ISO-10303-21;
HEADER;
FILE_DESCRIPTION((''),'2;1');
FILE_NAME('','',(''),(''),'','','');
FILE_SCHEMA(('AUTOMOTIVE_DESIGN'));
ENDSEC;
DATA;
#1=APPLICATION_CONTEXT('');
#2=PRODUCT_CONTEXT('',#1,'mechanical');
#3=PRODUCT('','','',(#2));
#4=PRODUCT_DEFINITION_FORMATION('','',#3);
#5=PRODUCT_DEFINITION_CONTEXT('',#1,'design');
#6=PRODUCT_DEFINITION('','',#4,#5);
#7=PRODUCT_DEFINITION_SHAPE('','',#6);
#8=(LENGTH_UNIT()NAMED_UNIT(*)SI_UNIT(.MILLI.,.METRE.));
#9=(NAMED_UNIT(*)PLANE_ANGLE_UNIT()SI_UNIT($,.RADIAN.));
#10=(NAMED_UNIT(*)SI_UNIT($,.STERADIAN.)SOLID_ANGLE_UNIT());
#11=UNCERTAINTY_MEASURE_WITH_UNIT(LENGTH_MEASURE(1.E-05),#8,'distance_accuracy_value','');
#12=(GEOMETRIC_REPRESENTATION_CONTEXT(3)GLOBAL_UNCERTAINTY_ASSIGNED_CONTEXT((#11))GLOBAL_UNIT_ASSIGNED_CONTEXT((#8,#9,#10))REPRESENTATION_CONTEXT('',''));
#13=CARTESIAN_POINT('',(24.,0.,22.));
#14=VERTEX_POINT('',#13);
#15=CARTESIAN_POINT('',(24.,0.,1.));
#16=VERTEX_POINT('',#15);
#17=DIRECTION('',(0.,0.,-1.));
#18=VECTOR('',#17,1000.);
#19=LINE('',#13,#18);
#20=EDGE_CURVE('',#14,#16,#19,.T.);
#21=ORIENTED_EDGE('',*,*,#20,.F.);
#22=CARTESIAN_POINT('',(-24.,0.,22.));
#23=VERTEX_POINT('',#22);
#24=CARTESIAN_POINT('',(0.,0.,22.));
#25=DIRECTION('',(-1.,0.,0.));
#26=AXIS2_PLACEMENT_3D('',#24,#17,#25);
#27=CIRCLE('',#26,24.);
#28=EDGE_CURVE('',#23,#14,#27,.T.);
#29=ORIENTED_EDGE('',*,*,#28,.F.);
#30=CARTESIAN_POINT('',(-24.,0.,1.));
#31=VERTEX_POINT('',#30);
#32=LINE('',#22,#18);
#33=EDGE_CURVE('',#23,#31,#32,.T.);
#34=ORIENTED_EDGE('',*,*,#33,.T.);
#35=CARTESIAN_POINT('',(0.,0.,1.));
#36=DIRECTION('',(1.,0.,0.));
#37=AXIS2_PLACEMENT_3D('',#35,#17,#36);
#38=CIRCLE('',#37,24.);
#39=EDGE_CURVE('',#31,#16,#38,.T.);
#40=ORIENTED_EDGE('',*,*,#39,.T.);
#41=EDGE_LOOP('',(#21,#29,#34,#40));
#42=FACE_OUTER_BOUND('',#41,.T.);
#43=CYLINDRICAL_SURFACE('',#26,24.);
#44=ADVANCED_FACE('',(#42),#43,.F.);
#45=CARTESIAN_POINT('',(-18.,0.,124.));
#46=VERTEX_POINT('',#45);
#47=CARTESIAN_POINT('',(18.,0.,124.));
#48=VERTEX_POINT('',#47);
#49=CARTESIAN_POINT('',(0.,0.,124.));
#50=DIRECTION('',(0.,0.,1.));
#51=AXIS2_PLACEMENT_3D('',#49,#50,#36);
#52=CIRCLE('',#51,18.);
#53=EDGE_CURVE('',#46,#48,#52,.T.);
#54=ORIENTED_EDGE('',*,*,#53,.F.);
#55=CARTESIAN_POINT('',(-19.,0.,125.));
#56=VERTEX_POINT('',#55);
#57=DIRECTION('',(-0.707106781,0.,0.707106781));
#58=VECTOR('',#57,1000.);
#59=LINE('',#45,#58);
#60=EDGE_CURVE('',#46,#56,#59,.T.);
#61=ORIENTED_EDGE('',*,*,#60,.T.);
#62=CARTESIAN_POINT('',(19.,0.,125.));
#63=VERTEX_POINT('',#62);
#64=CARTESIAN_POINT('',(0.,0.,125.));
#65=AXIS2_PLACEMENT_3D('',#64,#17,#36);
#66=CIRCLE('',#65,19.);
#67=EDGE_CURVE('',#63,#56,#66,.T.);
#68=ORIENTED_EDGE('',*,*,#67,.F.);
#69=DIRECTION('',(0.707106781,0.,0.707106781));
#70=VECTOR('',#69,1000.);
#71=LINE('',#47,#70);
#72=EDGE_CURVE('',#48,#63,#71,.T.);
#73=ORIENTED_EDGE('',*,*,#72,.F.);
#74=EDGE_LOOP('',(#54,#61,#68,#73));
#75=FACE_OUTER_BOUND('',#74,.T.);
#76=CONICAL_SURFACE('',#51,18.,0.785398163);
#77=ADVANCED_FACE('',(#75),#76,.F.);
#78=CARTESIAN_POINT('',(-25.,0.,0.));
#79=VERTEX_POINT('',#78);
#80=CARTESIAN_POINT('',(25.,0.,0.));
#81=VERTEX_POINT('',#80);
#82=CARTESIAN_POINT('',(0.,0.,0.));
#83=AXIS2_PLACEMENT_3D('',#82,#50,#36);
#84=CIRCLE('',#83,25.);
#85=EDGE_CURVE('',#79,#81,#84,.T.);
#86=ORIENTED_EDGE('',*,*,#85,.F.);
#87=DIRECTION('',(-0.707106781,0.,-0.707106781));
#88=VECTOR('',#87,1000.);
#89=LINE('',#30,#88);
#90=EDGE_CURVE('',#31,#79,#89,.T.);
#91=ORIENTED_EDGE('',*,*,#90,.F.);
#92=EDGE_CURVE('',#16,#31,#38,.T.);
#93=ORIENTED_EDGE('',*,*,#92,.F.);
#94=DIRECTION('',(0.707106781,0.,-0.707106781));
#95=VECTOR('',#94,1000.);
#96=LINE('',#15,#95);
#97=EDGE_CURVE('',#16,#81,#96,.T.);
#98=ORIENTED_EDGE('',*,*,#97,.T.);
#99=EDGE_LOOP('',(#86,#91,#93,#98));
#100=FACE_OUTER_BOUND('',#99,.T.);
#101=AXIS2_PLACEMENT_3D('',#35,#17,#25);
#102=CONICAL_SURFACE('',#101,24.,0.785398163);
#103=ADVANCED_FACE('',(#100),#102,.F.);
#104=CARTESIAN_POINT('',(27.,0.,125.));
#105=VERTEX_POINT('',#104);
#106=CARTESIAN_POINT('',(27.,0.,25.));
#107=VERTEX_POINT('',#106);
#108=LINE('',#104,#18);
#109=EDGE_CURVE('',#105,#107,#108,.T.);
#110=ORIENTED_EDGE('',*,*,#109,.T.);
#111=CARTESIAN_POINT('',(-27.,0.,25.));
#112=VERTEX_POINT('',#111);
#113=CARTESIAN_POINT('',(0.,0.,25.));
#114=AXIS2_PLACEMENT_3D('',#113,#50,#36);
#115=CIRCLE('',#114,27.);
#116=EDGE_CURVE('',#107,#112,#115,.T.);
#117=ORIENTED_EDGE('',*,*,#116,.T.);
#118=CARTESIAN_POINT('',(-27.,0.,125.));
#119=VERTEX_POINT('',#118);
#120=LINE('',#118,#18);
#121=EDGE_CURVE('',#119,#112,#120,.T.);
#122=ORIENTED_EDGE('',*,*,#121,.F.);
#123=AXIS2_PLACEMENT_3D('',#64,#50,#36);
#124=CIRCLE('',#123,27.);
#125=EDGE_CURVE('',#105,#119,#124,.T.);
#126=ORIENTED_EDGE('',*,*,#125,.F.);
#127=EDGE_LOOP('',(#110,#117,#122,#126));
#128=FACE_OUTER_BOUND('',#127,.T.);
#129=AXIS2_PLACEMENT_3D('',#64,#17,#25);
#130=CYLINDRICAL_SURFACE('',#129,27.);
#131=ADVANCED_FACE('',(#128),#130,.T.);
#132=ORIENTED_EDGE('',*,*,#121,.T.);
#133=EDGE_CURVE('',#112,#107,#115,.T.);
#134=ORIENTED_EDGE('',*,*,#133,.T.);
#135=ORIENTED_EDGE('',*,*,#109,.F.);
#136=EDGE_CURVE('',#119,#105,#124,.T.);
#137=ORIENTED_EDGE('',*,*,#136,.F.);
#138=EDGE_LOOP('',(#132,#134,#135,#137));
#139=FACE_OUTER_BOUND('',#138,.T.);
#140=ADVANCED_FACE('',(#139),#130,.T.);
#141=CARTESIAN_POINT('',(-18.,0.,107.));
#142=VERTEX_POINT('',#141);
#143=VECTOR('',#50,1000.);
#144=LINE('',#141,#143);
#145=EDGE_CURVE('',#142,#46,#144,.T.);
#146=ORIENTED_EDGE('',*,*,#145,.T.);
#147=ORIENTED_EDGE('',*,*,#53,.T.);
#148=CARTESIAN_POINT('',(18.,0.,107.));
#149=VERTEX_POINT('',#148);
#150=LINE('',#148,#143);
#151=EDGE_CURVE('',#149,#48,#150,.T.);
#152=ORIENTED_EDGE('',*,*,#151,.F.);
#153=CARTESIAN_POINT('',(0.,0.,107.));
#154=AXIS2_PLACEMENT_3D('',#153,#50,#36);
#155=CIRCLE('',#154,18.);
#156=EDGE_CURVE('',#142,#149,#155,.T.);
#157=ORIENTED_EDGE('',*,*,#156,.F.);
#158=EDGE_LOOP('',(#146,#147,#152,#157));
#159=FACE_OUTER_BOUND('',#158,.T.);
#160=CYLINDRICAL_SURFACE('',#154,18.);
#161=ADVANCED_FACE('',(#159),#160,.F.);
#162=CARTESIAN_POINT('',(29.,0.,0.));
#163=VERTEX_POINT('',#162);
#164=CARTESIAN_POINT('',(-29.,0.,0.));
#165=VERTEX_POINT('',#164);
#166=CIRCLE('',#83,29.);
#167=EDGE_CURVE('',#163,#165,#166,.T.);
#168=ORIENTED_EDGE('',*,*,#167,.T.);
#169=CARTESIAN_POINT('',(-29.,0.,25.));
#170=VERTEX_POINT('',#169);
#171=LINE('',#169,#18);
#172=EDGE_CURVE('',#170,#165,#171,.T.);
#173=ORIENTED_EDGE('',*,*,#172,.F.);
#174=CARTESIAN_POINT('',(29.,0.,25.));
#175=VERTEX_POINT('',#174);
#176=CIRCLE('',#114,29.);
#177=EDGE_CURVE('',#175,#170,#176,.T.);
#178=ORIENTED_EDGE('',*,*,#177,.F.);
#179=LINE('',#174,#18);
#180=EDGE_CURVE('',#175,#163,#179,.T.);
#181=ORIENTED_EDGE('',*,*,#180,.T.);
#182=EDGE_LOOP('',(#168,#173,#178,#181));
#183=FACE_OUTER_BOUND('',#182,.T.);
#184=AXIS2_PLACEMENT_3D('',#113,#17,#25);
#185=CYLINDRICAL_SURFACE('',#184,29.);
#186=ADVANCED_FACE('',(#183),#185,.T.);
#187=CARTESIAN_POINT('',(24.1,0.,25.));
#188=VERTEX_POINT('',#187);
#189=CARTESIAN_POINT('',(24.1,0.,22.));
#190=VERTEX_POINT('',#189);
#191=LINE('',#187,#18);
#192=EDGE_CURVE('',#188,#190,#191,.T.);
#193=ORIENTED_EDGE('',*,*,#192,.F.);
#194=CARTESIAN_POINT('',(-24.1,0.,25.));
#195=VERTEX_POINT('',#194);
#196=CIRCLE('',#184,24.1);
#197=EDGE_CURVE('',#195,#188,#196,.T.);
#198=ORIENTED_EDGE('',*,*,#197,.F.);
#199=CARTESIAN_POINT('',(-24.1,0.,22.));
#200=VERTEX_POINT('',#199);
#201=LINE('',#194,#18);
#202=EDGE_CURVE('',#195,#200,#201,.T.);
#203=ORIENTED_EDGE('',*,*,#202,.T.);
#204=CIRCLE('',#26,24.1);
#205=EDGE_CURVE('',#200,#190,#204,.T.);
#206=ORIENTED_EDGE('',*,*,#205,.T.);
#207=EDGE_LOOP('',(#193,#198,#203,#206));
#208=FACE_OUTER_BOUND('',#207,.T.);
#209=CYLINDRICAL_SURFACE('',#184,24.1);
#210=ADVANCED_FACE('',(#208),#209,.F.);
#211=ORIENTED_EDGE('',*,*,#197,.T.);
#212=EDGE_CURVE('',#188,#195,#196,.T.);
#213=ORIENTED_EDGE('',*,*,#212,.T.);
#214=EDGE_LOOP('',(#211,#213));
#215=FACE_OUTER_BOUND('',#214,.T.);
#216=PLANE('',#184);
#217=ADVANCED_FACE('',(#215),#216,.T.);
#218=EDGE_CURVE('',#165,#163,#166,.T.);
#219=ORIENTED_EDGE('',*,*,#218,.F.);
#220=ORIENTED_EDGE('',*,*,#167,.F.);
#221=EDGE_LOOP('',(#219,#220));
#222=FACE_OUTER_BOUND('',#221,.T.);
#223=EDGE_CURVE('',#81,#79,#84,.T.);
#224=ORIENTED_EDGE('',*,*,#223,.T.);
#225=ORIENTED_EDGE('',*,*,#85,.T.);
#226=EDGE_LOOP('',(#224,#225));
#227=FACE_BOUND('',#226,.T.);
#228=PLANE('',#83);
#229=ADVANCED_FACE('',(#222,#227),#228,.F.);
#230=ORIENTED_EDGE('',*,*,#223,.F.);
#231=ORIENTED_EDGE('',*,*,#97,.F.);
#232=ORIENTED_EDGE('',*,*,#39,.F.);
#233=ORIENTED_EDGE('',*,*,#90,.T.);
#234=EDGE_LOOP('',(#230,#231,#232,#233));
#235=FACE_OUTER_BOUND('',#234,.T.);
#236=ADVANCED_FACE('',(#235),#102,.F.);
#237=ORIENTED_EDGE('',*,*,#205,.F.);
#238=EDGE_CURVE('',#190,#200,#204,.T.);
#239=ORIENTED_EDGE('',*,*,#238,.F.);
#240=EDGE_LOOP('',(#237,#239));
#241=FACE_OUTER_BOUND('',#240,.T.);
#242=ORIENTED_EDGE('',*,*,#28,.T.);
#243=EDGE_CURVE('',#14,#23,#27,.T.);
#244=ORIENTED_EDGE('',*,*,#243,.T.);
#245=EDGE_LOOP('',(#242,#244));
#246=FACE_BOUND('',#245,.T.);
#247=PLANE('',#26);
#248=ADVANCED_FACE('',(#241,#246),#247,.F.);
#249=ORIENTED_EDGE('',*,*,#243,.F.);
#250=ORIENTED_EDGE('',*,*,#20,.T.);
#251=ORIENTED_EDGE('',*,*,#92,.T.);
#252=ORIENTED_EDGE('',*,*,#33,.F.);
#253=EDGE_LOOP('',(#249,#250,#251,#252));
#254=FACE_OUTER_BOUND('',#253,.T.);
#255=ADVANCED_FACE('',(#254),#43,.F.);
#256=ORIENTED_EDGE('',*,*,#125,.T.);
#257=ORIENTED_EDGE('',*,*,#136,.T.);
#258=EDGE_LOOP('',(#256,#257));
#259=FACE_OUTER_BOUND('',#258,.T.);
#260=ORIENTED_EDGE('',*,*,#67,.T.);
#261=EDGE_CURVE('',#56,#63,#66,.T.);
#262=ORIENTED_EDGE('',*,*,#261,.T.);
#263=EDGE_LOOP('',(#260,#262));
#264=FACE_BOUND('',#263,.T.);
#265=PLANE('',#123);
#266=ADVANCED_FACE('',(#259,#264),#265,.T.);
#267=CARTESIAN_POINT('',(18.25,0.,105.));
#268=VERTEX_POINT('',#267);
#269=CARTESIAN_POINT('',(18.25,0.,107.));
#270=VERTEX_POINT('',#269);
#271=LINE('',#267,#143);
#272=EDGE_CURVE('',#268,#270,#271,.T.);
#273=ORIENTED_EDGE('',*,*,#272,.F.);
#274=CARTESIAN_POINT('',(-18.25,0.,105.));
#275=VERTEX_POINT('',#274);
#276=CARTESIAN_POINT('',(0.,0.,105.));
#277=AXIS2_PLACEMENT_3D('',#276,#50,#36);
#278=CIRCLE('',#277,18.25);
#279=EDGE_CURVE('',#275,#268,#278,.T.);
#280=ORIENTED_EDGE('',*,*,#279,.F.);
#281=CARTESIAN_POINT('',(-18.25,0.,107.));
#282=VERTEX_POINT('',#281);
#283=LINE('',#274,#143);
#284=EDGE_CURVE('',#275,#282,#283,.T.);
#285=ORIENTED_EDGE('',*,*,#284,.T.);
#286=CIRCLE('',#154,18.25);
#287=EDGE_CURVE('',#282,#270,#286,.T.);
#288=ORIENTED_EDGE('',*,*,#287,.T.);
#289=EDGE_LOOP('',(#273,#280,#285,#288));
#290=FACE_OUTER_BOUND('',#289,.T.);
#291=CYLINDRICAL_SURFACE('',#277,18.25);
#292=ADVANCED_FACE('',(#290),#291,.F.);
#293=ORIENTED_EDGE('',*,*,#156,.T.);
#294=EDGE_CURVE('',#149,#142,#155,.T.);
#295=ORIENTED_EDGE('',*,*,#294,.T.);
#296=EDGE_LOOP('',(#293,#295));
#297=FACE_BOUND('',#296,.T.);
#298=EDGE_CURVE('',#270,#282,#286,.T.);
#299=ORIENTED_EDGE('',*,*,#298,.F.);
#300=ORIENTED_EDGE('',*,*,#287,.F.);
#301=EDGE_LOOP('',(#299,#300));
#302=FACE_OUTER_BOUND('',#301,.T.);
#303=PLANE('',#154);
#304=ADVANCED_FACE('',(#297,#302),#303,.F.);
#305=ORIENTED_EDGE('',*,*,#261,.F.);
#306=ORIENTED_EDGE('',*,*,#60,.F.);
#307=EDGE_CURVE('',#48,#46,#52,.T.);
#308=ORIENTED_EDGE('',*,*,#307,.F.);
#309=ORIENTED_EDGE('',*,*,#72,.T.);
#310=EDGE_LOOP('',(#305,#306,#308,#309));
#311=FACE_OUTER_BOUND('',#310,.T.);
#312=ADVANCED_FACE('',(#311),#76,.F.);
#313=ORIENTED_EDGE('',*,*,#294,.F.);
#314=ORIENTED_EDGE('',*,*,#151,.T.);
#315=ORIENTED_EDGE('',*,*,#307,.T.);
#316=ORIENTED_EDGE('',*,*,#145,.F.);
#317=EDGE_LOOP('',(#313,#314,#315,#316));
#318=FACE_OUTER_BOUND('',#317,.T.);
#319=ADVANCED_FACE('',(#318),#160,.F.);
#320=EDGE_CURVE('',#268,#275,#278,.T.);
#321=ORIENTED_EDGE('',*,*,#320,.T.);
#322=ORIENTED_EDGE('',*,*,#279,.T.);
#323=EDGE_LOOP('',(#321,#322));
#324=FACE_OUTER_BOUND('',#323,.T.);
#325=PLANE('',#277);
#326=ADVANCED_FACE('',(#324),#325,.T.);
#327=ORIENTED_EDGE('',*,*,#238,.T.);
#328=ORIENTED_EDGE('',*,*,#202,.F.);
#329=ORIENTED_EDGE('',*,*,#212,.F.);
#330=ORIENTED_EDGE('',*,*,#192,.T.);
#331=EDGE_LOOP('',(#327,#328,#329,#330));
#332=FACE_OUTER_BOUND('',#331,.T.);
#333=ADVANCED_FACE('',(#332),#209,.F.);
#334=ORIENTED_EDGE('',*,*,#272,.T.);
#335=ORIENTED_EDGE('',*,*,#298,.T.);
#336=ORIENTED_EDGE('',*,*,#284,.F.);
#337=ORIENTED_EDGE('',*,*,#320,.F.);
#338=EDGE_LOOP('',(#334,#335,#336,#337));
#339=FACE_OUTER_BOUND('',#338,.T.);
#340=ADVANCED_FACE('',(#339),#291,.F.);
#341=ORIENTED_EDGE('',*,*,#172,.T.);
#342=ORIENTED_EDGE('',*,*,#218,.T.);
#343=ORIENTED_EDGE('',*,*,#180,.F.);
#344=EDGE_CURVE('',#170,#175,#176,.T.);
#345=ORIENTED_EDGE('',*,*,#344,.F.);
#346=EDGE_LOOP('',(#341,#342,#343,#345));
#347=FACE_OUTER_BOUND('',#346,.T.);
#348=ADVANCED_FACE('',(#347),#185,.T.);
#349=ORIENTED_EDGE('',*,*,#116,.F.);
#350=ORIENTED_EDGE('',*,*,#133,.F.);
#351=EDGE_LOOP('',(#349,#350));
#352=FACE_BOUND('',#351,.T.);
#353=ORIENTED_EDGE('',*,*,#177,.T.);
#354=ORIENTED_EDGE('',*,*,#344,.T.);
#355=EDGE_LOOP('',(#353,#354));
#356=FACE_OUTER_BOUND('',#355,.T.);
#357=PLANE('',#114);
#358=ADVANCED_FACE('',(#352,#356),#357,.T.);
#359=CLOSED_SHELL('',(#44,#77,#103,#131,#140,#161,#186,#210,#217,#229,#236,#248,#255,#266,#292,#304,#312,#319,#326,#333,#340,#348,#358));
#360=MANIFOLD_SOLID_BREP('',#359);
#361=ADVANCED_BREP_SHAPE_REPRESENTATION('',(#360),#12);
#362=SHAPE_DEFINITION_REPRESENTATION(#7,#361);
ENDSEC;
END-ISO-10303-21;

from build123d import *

# Parameters (mm, degrees)
SKETCH1_R           = 29
BOSS_EXTRUDE1_DEPTH = 25
SKETCH2_R           = 27
BOSS_EXTRUDE2_DEPTH = 100
SKETCH7_R           = 24
CUT_EXTRUDE4_DEPTH  = 22
SKETCH8_R           = 24.1
CUT_EXTRUDE5_DEPTH  = 3
CHAMFER1_SIZE       = 1
SKETCH9_R           = 18
CUT_EXTRUDE6_DEPTH  = 18
SKETCH10_R          = 18.25
CUT_EXTRUDE7_DEPTH  = 2
CHAMFER2_SIZE       = 1


with BuildPart() as part:
    # Sketch1 → Boss-Extrude1 (new body)
    with BuildSketch(Plane.XY):
        Circle(SKETCH1_R)
    extrude(amount=BOSS_EXTRUDE1_DEPTH)

    # Sketch2 → Boss-Extrude2 (add)
    with BuildSketch(Plane.XY.offset(25)):
        Circle(SKETCH2_R)
    extrude(amount=BOSS_EXTRUDE2_DEPTH)

    # Sketch7 → Cut-Extrude4 (cut)
    with BuildSketch(Plane(origin=(0, 0, 0), x_dir=(-1, 0, 0), z_dir=(0, 0, -1))):
        Circle(SKETCH7_R)
    extrude(amount=-CUT_EXTRUDE4_DEPTH, mode=Mode.SUBTRACT)

    # Sketch8 → Cut-Extrude5 (cut)
    with BuildSketch(Plane(origin=(0, 0, 22), x_dir=(-1, 0, 0), z_dir=(0, 0, -1))):
        Circle(SKETCH8_R)
    extrude(amount=-CUT_EXTRUDE5_DEPTH, mode=Mode.SUBTRACT)

    # Chamfer1
    chamfer1_edges = [part.edges().sort_by_distance(p)[0] for p in [
        (24, 0, 0),
    ]]
    chamfer(chamfer1_edges, length=CHAMFER1_SIZE)

    # Sketch9 → Cut-Extrude6 (cut)
    with BuildSketch(Plane.XY.offset(125)):
        Circle(SKETCH9_R)
    extrude(amount=-CUT_EXTRUDE6_DEPTH, mode=Mode.SUBTRACT)

    # Sketch10 → Cut-Extrude7 (cut)
    with BuildSketch(Plane.XY.offset(107)):
        Circle(SKETCH10_R)
    extrude(amount=-CUT_EXTRUDE7_DEPTH, mode=Mode.SUBTRACT)

    # Chamfer2
    chamfer2_edges = [part.edges().sort_by_distance(p)[0] for p in [
        (-18, 0, 125),
    ]]
    chamfer(chamfer2_edges, length=CHAMFER2_SIZE)


solid = part.part
